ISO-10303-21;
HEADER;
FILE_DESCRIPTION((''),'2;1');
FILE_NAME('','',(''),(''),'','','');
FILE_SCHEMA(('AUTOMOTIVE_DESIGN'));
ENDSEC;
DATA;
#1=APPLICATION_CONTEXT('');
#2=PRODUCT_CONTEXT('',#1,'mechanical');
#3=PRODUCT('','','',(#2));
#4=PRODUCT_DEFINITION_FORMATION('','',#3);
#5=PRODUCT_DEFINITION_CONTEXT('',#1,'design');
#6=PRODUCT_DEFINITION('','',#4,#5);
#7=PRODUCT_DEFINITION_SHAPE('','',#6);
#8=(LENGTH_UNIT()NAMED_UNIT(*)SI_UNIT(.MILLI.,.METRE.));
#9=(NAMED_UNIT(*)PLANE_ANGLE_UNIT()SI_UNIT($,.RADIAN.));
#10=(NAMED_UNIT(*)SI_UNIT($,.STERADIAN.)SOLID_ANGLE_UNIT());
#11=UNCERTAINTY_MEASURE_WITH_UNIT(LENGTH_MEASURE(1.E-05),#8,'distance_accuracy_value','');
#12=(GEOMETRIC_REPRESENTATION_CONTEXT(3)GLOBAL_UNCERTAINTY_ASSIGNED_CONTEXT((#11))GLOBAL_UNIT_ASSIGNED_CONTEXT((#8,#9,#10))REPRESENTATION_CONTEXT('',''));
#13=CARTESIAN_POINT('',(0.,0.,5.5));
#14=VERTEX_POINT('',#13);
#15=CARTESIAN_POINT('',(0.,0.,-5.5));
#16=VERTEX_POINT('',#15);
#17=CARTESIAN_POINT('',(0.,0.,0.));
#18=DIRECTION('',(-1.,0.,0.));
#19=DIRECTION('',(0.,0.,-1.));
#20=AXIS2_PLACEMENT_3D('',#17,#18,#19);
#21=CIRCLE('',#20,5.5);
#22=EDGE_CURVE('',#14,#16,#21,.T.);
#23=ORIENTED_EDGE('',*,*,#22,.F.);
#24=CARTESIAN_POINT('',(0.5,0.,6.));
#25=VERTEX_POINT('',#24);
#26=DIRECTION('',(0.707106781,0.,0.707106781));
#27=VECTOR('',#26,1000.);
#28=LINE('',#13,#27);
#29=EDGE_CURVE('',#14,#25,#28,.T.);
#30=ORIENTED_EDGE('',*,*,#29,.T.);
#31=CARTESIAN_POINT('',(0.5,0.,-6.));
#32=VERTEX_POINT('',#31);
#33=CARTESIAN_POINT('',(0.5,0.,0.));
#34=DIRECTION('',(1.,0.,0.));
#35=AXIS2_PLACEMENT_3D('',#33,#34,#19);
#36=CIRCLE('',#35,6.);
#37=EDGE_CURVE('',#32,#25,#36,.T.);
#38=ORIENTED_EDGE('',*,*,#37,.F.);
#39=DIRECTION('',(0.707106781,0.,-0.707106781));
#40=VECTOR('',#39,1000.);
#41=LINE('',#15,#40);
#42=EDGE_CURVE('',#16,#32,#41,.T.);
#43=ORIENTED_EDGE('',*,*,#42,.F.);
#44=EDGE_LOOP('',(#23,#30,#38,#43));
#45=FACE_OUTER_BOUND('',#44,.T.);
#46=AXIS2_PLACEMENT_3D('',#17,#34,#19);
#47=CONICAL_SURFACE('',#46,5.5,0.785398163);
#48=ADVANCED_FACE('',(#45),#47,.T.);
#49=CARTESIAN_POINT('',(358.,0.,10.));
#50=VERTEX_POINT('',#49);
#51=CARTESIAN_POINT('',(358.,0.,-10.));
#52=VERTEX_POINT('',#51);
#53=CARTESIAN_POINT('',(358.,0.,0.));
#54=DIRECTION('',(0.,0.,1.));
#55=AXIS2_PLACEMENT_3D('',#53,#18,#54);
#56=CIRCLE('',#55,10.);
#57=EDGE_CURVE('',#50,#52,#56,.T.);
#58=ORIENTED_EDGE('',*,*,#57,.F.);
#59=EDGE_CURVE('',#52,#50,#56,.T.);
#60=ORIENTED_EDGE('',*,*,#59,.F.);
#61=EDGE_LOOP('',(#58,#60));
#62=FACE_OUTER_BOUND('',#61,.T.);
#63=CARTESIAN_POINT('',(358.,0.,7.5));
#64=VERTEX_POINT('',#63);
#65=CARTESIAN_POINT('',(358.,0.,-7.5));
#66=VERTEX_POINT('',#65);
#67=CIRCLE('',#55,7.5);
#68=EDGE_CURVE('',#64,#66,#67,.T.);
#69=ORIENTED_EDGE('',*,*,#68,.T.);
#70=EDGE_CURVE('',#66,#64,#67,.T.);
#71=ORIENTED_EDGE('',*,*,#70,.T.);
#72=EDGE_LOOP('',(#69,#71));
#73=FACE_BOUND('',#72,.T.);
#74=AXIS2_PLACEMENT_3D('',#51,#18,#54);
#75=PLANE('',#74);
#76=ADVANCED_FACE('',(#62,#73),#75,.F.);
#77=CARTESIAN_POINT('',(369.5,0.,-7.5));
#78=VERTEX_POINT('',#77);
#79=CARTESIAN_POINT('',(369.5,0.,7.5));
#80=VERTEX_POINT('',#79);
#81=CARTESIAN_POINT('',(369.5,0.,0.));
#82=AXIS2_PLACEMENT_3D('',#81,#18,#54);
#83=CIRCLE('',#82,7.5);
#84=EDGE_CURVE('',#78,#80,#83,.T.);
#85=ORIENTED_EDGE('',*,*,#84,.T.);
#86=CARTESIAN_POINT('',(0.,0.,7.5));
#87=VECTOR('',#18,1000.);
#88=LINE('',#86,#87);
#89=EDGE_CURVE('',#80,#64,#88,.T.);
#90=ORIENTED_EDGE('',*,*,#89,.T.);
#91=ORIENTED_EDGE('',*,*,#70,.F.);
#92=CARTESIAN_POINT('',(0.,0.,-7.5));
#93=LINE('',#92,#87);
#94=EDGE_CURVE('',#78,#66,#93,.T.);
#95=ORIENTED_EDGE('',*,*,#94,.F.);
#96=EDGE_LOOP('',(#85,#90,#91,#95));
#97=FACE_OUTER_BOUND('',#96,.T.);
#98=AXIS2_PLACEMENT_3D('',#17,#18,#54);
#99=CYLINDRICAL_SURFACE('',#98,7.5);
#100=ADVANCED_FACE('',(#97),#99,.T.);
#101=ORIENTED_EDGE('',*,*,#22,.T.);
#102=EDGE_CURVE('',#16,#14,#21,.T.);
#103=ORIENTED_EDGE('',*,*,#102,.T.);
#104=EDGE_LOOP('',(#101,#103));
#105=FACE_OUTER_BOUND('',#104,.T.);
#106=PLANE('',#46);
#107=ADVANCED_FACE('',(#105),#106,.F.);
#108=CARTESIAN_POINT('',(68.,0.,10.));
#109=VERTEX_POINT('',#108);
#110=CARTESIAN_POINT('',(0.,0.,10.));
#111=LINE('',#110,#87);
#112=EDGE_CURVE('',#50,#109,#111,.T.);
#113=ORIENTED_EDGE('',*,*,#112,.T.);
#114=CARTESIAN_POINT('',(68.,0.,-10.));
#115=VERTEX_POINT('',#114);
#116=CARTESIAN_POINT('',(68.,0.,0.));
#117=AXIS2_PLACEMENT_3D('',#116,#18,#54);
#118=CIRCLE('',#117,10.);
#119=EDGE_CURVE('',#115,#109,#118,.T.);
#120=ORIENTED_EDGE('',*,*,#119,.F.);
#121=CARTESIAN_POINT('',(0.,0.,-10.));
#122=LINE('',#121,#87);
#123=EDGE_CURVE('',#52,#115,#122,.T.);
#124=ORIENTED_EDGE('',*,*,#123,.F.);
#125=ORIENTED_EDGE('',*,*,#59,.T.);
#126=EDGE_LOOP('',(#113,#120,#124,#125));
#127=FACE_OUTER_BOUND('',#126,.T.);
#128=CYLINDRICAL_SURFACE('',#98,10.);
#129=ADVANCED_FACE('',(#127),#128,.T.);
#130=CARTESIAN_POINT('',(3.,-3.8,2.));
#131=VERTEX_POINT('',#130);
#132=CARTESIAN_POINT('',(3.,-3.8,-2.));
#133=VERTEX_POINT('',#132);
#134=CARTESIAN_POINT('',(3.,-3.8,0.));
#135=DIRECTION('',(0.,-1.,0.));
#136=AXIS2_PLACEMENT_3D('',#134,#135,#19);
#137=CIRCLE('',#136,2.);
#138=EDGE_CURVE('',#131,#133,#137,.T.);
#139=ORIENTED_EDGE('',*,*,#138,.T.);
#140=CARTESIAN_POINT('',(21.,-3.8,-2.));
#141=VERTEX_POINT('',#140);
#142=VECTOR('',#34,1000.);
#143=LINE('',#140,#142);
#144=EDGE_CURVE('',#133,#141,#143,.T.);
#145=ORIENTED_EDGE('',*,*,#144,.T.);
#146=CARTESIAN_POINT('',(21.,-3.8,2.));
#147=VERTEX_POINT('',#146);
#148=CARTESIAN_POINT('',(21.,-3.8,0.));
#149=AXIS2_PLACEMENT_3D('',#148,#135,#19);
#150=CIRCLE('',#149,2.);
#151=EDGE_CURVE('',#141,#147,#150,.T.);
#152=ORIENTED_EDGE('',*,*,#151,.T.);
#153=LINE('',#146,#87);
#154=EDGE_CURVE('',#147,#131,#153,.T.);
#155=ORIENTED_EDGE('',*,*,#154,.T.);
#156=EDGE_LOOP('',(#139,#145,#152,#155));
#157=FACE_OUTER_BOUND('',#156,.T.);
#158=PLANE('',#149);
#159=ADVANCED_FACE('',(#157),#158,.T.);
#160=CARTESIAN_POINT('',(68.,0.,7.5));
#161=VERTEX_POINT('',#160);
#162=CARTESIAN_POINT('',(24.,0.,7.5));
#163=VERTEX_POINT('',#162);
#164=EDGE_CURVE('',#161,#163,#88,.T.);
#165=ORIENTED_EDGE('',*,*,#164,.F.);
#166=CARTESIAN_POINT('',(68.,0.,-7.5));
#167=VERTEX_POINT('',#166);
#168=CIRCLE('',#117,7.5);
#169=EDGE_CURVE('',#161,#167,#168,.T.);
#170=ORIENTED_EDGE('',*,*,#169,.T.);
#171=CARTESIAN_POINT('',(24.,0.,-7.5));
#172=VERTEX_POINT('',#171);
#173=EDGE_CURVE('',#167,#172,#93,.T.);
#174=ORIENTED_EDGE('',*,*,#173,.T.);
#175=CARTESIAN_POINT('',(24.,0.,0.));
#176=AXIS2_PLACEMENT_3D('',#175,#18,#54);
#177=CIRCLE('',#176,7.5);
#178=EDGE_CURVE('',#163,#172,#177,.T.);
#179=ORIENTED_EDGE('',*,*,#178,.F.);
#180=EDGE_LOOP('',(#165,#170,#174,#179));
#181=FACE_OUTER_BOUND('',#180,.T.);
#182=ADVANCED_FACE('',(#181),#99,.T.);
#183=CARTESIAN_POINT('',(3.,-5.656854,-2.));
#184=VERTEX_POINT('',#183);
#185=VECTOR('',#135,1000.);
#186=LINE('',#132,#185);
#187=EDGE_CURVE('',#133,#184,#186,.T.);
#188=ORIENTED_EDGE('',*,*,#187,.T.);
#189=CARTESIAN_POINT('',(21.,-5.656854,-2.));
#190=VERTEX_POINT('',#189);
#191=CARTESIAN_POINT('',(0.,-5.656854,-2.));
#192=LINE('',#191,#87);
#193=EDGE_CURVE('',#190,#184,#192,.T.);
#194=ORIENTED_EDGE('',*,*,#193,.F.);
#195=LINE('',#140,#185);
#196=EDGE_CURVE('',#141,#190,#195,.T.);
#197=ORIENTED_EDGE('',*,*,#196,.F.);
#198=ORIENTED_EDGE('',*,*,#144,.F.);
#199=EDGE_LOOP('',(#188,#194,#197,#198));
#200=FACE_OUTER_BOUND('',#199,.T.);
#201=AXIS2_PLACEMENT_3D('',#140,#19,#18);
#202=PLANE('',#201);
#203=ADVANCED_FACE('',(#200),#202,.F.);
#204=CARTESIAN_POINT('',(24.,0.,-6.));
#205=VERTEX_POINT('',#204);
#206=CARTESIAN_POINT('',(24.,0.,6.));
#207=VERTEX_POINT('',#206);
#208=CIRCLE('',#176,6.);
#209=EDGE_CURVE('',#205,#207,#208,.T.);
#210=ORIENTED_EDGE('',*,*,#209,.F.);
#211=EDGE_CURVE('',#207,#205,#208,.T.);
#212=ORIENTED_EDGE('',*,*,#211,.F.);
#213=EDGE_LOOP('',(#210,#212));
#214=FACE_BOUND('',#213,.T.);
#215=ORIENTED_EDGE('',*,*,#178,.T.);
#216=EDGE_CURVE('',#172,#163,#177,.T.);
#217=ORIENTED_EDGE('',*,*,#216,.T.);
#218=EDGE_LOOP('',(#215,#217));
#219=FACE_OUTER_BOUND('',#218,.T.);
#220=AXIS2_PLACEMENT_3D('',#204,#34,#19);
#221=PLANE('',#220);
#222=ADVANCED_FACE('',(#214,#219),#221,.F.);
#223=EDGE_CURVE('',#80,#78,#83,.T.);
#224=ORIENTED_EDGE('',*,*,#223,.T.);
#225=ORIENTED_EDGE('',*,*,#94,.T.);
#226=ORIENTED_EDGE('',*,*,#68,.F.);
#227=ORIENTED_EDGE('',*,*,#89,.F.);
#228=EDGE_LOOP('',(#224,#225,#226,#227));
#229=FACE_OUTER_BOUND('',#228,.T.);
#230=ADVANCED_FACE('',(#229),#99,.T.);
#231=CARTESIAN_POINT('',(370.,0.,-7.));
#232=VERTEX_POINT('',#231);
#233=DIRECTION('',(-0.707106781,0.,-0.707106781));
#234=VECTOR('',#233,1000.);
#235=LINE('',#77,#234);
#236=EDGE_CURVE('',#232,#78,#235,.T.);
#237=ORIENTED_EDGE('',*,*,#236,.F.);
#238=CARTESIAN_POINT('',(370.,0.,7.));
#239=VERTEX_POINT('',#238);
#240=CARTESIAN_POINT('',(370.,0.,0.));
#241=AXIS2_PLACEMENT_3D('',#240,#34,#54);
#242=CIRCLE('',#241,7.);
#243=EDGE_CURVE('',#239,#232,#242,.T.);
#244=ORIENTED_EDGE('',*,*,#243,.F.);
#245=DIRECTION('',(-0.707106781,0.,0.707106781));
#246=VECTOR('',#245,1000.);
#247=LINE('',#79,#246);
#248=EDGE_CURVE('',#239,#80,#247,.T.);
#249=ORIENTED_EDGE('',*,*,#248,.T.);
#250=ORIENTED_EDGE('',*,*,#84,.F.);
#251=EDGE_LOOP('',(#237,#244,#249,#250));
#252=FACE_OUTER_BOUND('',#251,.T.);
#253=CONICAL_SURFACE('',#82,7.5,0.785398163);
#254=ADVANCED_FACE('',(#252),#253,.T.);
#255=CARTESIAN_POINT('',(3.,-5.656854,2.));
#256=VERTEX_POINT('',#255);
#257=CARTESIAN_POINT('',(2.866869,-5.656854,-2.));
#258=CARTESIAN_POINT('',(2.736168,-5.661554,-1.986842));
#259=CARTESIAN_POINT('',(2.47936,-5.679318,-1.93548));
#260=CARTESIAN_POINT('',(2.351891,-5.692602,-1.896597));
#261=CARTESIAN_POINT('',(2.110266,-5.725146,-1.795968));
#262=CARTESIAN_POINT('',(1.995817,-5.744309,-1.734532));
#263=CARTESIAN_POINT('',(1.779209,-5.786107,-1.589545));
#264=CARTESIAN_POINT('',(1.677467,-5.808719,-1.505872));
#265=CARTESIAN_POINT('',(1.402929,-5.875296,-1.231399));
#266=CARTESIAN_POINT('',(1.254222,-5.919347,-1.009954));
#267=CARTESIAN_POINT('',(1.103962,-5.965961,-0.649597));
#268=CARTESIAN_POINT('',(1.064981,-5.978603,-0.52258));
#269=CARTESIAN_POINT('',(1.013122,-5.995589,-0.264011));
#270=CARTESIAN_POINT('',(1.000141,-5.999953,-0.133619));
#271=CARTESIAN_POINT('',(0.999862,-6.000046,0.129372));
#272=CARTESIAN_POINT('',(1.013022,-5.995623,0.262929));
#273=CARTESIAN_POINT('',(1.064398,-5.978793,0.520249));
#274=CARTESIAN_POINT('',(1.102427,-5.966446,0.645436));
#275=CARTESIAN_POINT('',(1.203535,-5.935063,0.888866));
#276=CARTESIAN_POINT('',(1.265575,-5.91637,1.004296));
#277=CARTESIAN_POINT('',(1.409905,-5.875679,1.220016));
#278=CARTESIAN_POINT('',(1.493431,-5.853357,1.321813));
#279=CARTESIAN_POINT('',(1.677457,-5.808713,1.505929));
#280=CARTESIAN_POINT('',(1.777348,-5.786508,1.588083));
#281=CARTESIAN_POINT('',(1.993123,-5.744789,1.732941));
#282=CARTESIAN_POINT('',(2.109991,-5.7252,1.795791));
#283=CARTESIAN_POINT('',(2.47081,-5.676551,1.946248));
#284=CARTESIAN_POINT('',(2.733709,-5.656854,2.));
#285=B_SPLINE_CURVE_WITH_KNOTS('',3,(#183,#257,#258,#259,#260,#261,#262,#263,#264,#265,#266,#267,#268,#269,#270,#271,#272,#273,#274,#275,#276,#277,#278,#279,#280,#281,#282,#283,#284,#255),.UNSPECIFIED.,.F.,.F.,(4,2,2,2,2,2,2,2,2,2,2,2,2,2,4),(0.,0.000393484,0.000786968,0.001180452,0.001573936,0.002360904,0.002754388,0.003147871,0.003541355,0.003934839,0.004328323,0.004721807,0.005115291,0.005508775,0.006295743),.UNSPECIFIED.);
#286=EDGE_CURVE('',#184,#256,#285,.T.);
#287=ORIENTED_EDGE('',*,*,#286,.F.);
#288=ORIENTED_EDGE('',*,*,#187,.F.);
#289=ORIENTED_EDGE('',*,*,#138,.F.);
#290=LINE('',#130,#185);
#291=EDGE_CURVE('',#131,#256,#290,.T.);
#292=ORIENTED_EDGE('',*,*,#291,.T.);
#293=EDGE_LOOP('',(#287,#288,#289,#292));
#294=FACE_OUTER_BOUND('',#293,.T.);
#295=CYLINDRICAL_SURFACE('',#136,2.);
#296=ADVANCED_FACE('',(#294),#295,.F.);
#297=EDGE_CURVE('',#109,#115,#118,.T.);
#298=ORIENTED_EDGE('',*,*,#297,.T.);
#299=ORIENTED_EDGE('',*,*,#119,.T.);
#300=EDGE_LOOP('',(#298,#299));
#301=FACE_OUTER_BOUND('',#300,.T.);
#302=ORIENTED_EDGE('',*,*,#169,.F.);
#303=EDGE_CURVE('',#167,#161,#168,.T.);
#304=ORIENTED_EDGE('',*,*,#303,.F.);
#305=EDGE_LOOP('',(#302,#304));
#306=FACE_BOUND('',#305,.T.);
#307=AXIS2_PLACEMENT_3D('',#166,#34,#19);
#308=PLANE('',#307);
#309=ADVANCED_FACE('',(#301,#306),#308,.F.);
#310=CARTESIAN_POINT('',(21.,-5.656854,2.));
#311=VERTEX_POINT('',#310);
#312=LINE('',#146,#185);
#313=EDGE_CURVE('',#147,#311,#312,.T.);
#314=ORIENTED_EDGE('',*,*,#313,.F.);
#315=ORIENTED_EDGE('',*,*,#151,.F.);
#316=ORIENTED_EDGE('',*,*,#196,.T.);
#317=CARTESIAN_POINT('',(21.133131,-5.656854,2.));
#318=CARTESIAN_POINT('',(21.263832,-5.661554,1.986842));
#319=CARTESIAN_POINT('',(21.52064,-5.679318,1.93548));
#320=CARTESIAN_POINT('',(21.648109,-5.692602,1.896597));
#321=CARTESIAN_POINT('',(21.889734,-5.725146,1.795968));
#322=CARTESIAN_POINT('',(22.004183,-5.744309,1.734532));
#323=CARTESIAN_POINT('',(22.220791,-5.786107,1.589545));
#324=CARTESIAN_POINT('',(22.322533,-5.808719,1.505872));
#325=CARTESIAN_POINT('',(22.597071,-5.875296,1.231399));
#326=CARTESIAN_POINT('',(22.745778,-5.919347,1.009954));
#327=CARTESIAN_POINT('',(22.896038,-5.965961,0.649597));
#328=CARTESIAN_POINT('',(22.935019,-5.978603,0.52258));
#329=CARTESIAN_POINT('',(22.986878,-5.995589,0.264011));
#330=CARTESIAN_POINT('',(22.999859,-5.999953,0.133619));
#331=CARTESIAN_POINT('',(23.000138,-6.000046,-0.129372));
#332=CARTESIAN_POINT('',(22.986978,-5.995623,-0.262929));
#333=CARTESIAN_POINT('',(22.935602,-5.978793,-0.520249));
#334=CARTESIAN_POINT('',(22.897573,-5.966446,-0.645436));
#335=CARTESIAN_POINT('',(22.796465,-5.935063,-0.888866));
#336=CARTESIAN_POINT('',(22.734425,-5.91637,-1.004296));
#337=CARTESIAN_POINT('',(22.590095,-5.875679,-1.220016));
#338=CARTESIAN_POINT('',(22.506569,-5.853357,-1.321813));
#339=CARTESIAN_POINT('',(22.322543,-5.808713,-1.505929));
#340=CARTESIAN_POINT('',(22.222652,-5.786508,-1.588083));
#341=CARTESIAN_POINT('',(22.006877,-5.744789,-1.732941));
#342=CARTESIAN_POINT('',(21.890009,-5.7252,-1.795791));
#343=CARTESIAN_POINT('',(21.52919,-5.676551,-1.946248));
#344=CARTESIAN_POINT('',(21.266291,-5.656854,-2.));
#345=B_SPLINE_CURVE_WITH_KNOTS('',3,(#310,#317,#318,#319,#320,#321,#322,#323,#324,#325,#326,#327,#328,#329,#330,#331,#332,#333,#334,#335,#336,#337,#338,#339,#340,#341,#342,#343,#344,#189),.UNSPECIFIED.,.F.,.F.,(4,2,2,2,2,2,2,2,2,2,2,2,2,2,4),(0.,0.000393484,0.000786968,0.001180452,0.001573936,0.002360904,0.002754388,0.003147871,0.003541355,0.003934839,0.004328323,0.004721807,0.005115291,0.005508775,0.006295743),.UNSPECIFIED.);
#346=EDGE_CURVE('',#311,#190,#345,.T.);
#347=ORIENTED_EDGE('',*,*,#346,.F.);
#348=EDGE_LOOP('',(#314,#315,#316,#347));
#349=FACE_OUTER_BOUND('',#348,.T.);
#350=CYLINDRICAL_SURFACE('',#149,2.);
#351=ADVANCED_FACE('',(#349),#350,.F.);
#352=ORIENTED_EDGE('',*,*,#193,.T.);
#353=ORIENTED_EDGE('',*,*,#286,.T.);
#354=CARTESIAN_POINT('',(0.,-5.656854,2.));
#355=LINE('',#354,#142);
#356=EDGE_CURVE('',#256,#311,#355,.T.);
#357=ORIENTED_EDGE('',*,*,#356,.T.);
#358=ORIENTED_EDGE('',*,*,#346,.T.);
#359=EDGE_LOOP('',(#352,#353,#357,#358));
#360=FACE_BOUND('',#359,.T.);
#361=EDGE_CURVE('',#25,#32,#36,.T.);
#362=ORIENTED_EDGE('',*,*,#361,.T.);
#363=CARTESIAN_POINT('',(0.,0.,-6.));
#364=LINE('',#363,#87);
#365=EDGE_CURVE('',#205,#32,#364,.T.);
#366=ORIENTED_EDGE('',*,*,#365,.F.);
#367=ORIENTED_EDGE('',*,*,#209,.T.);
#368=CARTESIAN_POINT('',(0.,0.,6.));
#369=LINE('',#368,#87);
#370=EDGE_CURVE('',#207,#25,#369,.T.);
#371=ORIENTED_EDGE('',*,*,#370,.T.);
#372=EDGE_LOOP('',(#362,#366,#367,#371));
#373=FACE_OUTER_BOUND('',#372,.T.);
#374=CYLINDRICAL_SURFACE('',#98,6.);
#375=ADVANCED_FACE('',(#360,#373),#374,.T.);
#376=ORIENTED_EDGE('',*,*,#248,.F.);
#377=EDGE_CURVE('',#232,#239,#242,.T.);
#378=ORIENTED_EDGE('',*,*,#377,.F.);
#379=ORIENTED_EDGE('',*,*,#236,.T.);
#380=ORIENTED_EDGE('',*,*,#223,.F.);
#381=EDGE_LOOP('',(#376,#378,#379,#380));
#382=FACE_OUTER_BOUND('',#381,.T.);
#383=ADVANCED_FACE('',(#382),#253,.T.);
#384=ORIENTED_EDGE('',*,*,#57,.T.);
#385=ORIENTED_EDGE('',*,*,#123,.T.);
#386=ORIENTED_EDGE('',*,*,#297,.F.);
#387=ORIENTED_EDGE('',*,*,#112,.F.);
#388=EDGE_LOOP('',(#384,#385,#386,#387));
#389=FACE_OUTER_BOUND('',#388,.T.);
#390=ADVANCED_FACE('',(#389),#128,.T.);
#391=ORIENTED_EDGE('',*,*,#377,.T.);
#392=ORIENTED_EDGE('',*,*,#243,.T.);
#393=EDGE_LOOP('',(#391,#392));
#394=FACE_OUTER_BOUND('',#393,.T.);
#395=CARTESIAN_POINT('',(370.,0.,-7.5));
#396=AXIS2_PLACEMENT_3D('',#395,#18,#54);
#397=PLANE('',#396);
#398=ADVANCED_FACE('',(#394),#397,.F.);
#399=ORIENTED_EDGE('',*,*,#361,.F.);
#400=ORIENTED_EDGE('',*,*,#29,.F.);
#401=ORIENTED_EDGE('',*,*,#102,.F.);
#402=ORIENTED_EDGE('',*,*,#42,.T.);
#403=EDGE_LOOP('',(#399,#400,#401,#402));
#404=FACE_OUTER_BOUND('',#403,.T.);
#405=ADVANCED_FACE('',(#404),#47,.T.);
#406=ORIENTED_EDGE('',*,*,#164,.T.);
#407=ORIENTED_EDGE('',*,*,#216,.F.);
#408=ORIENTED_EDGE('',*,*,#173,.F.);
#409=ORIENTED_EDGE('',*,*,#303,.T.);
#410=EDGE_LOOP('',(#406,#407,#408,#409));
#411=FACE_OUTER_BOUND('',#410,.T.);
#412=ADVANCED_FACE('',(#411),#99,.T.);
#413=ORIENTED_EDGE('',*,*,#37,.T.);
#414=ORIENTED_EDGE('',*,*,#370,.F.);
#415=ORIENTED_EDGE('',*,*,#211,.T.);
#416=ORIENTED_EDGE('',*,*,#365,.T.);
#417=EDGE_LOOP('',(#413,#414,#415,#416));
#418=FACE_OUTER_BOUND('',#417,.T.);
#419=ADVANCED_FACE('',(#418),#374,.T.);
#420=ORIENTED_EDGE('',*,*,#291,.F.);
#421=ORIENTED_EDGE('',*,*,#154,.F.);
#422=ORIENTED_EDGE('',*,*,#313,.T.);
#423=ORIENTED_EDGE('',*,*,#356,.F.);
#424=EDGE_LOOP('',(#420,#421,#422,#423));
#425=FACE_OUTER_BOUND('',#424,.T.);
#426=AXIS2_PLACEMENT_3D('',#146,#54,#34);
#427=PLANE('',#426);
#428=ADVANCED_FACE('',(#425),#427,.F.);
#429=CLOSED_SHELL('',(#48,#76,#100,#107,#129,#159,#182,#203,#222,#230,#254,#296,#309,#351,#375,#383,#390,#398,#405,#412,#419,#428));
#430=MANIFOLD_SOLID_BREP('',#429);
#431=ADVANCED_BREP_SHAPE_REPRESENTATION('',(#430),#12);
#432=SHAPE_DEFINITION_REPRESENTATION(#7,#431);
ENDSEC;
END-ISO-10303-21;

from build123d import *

# Parameters (mm, degrees)
CUT_EXTRUDE_1_DEPTH = 2.2
CHAMFER_1_SIZE      = 0.5


with BuildPart() as part:
    # 草图1 → 旋转1 (revolve)
    with BuildSketch(Plane(origin=(0, 0, 0), x_dir=(1, 0, 0), z_dir=(0, 1, 0)), mode=Mode.PRIVATE) as revolve_1_sk:
        Polygon((0, 0), (0, 6), (24, 6), (24, 7.5), (68, 7.5), (68, 10), (358, 10), (358, 7.5), (370, 7.5), (370, 0), align=None)
    revolve(revolve_1_sk.sketch.rotate(Axis((0, 0, 0), (1, 0, 0)), 180), axis=Axis((0, 0, 0), (1, 0, 0)))

    # 草图2 → 切除-拉伸1 (cut)
    with BuildSketch(Plane(origin=(0, -6, 0), x_dir=(-1, 0, 0), z_dir=(0, -1, 0))):
        with BuildLine():
            Line((-21, 2), (-3, 2))
            ThreePointArc((-3, 2), (-1, 0), (-3, -2))
            Line((-3, -2), (-21, -2))
            ThreePointArc((-21, -2), (-23, 0), (-21, 2))
        make_face()
    extrude(amount=-CUT_EXTRUDE_1_DEPTH, mode=Mode.SUBTRACT)

    # 倒角1
    chamfer_1_edges = [part.edges().sort_by_distance(p)[0] for p in [
        (0, 0, -6),
        (370, 0, -7.5),
    ]]
    chamfer(chamfer_1_edges, length=CHAMFER_1_SIZE)


solid = part.part
